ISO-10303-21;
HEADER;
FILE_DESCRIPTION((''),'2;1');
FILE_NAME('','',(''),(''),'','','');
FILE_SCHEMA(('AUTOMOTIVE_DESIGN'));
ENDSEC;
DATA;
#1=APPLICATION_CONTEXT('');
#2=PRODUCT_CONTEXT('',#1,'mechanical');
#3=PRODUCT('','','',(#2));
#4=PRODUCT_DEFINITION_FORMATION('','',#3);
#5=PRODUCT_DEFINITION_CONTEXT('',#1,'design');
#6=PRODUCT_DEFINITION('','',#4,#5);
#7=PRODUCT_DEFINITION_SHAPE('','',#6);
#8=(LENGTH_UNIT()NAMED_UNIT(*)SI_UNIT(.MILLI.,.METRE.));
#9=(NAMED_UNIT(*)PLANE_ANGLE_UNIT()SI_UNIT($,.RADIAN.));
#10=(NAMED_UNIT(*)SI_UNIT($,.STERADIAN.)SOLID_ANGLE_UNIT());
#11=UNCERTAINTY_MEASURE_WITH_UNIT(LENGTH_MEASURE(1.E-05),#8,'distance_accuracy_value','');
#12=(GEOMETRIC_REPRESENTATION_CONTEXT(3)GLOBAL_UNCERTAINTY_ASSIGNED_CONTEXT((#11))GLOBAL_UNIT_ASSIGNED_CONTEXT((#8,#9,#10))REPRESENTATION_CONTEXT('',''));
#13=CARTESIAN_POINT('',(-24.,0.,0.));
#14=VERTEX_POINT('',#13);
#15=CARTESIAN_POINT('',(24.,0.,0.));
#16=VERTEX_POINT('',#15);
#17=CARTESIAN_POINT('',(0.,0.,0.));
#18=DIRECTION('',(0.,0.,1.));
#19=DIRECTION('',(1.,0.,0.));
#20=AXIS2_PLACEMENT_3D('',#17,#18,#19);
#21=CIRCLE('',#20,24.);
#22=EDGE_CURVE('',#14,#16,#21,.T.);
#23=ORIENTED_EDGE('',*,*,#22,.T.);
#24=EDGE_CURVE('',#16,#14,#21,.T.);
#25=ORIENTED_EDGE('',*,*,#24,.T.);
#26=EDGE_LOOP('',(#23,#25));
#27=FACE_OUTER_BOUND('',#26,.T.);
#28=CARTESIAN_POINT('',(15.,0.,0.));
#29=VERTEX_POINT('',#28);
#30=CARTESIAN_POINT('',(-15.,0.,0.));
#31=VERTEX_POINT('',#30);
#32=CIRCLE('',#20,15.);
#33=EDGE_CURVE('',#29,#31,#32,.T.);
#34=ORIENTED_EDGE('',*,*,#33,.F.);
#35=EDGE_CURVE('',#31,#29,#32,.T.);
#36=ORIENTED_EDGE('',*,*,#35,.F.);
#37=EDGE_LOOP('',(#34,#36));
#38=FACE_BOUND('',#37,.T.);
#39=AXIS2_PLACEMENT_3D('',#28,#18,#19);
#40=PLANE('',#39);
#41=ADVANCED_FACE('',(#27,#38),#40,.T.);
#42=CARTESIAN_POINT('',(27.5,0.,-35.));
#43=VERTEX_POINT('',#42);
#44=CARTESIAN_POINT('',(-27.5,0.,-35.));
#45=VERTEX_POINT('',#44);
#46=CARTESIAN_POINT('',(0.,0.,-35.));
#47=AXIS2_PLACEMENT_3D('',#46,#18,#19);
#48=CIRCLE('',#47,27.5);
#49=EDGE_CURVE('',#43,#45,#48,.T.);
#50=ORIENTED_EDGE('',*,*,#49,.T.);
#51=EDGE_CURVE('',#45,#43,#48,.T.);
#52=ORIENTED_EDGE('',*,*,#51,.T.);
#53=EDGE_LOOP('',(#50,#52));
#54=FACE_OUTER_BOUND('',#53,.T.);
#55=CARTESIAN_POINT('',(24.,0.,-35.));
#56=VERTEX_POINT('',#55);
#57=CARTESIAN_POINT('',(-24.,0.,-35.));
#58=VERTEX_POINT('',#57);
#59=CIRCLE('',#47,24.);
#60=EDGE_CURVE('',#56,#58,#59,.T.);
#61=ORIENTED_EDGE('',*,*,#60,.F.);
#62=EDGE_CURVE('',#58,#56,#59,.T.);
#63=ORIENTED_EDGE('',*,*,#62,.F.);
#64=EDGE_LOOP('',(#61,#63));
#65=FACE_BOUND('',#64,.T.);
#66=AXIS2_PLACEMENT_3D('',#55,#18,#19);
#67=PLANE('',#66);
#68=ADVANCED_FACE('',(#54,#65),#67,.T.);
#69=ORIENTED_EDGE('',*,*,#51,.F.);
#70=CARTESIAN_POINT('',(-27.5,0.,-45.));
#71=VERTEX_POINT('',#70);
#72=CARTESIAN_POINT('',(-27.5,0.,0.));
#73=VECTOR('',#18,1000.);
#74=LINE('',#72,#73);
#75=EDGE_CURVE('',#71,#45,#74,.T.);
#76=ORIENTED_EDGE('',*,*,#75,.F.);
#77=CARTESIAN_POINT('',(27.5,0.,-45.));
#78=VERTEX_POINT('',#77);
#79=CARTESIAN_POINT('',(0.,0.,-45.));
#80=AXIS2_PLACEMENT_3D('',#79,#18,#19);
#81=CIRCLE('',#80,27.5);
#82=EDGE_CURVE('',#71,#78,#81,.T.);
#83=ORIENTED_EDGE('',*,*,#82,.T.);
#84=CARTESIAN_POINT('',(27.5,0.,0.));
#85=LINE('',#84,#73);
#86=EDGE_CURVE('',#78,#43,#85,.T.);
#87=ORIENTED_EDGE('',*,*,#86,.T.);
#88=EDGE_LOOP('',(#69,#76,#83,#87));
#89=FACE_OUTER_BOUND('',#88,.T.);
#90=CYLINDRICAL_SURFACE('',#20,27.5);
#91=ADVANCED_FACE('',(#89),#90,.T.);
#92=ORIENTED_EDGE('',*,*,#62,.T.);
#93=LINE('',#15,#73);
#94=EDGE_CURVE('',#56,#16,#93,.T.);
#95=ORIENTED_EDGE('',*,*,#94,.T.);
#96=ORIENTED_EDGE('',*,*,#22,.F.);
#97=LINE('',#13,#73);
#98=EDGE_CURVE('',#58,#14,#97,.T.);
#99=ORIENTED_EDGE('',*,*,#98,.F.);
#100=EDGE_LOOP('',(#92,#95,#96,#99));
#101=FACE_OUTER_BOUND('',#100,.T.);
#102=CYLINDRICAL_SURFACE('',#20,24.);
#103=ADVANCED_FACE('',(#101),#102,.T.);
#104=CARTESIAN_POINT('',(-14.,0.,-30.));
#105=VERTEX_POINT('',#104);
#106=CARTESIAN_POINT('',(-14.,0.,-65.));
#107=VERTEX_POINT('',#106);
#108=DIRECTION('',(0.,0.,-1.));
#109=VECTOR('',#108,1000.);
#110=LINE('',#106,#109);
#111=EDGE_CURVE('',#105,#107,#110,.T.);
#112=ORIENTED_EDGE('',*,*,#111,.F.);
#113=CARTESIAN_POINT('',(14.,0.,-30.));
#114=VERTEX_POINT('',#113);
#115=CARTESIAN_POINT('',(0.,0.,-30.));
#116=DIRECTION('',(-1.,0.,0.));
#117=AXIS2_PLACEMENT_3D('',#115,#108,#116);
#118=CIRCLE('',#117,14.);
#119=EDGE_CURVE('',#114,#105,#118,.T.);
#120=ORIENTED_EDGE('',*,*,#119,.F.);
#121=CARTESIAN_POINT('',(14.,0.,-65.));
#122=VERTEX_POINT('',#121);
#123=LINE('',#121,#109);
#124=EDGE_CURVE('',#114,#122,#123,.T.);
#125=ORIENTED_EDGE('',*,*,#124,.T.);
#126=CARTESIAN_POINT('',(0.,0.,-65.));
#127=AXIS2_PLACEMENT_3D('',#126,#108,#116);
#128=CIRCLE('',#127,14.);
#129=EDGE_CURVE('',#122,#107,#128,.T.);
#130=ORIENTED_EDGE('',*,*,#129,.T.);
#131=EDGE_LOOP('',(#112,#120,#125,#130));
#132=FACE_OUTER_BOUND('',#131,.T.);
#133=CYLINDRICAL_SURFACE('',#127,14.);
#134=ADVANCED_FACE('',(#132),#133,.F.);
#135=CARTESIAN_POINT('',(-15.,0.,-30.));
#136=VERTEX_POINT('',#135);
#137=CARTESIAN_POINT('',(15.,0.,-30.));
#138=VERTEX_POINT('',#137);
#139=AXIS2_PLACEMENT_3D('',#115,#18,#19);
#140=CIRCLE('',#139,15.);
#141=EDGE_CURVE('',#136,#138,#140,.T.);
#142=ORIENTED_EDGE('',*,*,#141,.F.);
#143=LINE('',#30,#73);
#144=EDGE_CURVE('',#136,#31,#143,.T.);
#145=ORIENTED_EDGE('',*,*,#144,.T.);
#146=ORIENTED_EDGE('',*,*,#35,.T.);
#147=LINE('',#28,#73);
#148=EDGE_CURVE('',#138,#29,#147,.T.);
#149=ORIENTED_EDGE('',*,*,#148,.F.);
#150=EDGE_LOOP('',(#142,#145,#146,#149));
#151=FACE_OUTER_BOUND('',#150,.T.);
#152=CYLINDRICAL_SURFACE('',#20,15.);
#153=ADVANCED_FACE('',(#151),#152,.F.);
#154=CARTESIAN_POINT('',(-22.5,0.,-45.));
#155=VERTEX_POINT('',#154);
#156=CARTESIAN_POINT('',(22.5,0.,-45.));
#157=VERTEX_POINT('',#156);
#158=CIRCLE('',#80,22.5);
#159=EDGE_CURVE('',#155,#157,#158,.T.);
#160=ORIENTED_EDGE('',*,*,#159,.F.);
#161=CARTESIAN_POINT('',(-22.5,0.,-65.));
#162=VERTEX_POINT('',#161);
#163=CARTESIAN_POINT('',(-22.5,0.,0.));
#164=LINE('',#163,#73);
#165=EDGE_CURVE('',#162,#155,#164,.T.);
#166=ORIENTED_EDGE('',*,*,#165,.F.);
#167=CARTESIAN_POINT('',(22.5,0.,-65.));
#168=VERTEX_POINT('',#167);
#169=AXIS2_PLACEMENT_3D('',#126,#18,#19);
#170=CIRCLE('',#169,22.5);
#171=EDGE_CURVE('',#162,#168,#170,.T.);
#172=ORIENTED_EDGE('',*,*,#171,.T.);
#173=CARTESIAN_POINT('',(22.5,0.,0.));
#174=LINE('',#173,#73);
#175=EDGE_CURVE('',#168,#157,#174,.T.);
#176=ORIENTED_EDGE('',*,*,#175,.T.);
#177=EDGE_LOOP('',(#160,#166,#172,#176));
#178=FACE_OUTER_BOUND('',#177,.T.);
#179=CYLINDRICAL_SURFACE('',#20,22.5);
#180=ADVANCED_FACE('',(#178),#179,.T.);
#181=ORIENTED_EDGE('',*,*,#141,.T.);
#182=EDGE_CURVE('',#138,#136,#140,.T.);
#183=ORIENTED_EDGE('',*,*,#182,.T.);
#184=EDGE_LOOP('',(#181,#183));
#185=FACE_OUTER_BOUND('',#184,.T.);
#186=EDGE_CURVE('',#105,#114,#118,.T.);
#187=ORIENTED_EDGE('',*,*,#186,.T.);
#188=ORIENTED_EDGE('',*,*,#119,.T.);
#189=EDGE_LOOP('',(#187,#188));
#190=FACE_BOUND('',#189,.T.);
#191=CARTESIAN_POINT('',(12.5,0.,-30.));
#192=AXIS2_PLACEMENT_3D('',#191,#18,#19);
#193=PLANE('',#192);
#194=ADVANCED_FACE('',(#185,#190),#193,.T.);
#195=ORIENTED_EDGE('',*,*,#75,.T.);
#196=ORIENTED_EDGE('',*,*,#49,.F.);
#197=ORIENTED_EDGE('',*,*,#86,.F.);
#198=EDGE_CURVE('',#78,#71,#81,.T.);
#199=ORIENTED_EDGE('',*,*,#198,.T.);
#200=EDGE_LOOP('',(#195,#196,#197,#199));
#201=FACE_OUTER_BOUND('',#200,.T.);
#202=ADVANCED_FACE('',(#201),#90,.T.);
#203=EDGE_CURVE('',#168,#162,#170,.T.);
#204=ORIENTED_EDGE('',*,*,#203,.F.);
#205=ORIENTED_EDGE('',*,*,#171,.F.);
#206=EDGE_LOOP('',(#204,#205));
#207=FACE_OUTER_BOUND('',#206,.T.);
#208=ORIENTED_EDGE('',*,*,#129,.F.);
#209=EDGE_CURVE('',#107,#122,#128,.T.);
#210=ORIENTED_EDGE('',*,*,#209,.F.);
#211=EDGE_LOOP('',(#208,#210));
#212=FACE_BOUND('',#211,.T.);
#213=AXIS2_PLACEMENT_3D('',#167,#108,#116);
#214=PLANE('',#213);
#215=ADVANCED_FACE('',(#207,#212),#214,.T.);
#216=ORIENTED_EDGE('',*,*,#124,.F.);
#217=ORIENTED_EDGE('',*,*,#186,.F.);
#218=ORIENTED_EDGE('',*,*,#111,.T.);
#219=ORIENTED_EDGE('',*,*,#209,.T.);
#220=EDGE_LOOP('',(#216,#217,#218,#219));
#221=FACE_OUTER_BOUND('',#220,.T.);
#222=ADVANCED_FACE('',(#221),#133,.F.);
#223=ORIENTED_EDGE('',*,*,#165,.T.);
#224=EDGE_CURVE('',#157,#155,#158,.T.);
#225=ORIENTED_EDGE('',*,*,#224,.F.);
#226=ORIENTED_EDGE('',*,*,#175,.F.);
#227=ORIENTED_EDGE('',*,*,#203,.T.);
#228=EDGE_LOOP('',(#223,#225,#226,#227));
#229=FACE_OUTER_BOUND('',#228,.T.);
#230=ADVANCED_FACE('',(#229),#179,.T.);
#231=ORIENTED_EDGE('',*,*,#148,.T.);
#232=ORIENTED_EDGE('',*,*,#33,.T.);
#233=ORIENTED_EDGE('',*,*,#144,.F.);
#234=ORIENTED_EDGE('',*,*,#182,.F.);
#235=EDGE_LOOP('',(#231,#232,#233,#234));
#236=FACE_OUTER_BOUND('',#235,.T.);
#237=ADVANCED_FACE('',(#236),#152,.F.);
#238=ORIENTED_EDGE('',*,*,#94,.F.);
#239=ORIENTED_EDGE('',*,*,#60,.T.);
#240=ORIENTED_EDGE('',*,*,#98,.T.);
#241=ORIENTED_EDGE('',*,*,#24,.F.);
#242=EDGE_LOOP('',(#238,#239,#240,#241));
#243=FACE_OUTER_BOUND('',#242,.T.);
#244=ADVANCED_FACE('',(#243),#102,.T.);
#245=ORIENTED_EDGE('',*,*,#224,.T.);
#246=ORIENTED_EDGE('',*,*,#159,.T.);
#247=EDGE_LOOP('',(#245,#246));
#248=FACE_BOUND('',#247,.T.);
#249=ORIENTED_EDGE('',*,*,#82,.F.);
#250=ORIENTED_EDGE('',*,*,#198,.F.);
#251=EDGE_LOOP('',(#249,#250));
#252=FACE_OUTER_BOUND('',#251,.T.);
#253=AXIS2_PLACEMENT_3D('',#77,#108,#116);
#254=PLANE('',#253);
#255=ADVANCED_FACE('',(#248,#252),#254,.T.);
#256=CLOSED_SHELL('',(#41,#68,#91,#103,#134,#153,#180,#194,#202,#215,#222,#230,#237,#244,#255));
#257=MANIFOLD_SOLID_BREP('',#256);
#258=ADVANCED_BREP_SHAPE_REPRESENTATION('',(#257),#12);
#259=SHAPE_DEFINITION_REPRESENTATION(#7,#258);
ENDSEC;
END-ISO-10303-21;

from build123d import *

# Parameters (mm, degrees)
M30X2_0_TAPPED_HOLE1_D     = 28
M30X2_0_TAPPED_HOLE1_DEPTH = 35
M30X2_0_TAPPED_HOLE1_TIP   = 8.412048666


with BuildPart() as part:
    # Sketch1 → Revolve1 (revolve)
    with BuildSketch(Plane(origin=(0, 0, 0), x_dir=(1, 0, 0), z_dir=(0, 1, 0))):
        Polygon((15, 0), (24, 0), (24, 35), (27.5, 35), (27.5, 45), (22.5, 45), (22.5, 65), (12.5, 65), (12.5, 30), (15, 30), align=None)
    revolve(axis=Axis((0, 0, 0), (0, 0, -1)))

    # M30x2.0 Tapped Hole1
    with Locations(Plane(origin=(0, 0, -65), x_dir=(-1, 0, 0), z_dir=(0, 0, -1))):
        with Locations((0, 0)):
            Hole(M30X2_0_TAPPED_HOLE1_D / 2, depth=M30X2_0_TAPPED_HOLE1_DEPTH)
            with Locations((0, 0, -(M30X2_0_TAPPED_HOLE1_DEPTH + M30X2_0_TAPPED_HOLE1_TIP / 2))):  # 118° drill point
                Cone(0, M30X2_0_TAPPED_HOLE1_D / 2, M30X2_0_TAPPED_HOLE1_TIP, mode=Mode.SUBTRACT)


solid = part.part
